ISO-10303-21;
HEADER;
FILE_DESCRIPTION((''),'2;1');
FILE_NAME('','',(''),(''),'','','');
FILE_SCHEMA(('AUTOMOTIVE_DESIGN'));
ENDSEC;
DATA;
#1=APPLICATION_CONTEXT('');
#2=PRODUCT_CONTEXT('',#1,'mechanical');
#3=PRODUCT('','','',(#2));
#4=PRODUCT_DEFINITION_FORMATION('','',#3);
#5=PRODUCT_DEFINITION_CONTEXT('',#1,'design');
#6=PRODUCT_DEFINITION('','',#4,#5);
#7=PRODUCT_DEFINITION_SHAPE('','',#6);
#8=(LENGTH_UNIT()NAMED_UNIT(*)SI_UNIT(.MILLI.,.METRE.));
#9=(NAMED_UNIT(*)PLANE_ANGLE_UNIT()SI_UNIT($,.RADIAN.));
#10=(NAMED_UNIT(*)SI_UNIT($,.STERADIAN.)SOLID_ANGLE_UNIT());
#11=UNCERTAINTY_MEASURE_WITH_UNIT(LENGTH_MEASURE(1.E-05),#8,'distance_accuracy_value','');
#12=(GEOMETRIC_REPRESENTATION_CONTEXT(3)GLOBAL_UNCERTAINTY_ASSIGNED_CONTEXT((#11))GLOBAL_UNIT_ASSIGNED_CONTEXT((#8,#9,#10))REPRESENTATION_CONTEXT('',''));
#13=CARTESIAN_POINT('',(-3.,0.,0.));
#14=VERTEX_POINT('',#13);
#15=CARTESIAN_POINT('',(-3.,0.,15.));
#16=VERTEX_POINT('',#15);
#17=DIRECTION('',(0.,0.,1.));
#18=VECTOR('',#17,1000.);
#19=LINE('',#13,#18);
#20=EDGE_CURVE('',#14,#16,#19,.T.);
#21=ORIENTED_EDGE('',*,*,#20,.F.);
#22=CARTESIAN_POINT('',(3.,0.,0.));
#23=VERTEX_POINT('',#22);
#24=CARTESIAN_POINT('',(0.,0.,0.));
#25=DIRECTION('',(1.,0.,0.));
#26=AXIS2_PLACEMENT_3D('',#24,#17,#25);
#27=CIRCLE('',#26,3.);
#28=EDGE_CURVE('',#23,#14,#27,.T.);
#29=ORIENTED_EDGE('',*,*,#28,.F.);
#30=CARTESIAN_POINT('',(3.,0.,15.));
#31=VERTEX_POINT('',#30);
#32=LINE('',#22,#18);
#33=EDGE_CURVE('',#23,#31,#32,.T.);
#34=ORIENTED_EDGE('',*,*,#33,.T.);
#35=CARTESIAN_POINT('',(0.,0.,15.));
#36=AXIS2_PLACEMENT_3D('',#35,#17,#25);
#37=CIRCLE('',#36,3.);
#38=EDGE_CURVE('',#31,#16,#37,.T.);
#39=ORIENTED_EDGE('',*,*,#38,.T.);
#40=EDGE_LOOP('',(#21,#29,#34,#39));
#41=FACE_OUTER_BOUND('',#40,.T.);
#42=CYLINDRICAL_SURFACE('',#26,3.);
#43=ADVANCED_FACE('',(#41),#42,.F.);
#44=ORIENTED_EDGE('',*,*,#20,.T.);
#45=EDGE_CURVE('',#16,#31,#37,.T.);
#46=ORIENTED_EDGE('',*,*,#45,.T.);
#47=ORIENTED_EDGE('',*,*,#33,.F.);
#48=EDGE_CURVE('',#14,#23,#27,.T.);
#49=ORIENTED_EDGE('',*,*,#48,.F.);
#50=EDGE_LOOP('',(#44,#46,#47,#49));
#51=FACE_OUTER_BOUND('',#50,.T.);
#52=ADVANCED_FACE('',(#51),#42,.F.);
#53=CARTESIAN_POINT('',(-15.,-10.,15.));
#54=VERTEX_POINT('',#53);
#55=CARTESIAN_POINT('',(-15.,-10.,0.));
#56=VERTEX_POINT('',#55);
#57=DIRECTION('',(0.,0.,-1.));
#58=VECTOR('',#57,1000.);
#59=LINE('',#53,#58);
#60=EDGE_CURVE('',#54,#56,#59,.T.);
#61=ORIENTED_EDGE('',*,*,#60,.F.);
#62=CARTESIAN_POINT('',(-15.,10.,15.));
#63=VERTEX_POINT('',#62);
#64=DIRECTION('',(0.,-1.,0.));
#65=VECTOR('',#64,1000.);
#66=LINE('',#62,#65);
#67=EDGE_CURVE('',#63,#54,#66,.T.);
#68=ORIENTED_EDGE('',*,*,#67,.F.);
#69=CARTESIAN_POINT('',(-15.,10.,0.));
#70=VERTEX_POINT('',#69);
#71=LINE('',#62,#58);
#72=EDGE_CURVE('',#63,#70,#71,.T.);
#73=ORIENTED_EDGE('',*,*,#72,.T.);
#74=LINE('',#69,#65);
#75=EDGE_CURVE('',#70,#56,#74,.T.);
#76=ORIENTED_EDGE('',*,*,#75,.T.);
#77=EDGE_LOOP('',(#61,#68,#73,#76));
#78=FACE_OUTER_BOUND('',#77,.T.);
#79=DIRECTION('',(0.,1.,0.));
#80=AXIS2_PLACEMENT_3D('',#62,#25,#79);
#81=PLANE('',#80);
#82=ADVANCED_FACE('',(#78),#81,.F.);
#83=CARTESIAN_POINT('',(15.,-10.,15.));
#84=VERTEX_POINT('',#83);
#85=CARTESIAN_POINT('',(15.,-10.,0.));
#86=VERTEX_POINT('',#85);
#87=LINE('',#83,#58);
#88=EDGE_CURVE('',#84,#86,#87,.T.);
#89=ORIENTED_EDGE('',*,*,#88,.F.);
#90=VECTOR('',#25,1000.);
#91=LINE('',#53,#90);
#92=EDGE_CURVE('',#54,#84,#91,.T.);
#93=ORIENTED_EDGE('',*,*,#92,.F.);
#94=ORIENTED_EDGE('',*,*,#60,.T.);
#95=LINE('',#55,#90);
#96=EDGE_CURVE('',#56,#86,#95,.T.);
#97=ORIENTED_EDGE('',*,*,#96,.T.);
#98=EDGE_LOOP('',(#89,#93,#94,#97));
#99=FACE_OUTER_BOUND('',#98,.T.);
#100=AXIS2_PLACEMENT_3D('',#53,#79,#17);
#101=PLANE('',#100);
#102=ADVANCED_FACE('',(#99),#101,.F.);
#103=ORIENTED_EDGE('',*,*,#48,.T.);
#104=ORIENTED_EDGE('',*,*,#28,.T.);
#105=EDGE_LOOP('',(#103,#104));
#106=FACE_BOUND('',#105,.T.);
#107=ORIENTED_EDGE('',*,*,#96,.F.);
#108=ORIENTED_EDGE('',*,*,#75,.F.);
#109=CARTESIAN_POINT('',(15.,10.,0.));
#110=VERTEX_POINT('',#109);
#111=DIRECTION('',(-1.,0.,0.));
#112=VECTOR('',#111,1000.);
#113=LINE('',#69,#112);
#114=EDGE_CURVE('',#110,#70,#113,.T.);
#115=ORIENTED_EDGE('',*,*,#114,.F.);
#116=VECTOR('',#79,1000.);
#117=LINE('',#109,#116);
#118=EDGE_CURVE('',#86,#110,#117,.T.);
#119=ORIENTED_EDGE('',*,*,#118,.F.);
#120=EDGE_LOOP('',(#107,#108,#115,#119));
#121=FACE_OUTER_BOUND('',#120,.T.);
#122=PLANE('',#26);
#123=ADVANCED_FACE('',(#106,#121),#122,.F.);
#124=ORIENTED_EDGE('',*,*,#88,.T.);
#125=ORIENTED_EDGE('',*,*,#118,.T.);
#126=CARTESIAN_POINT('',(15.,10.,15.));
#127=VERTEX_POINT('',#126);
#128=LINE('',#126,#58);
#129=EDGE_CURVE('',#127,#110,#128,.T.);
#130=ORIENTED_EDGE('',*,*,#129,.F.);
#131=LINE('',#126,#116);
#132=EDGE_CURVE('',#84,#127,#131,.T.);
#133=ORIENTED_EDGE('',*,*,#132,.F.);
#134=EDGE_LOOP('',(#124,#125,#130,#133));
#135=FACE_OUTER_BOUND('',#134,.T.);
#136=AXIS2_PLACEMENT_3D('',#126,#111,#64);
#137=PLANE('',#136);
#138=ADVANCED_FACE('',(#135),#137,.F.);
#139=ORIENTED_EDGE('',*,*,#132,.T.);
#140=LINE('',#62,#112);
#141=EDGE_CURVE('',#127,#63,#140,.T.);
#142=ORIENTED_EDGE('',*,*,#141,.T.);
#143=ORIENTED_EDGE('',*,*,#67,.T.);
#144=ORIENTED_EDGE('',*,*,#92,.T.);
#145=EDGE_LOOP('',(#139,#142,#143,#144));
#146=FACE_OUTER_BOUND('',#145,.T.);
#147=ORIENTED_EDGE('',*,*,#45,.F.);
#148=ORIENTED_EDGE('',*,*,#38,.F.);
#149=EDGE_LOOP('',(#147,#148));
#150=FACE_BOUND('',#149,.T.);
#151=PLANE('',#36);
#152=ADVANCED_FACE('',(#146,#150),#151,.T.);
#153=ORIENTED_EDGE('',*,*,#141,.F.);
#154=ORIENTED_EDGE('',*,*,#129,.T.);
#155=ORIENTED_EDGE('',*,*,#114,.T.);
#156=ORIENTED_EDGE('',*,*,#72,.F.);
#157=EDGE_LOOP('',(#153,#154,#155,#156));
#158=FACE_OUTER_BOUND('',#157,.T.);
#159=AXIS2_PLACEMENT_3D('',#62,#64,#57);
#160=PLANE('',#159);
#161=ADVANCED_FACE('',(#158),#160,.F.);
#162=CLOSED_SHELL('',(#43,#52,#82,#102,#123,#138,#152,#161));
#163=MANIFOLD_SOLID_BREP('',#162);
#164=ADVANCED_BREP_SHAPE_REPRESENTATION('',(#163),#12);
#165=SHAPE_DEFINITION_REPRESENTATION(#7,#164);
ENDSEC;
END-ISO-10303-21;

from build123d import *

# Parameters (mm, degrees)
SKETCH1_W               = 30
SKETCH1_H               = 20
BOSS_EXTRUDE1_DEPTH     = 15
CUT_EXTRUDE1_DEPTH      = 24.452078799
CUT_EXTRUDE1_DEPTH_BACK = 24.452078799
SKETCH2_R               = 3


with BuildPart() as part:
    # Sketch1 → Boss-Extrude1 (new body)
    with BuildSketch(Plane.XY):
        Rectangle(SKETCH1_W, SKETCH1_H)
    extrude(amount=BOSS_EXTRUDE1_DEPTH)

    # Sketch2 → Cut-Extrude1 (cut, two sides: drawn at the far end of the back side and taken through both)
    with BuildSketch(Plane.XY.offset(15).offset(-CUT_EXTRUDE1_DEPTH_BACK)):
        Circle(SKETCH2_R)
    extrude(amount=CUT_EXTRUDE1_DEPTH + CUT_EXTRUDE1_DEPTH_BACK, mode=Mode.SUBTRACT)


solid = part.part
